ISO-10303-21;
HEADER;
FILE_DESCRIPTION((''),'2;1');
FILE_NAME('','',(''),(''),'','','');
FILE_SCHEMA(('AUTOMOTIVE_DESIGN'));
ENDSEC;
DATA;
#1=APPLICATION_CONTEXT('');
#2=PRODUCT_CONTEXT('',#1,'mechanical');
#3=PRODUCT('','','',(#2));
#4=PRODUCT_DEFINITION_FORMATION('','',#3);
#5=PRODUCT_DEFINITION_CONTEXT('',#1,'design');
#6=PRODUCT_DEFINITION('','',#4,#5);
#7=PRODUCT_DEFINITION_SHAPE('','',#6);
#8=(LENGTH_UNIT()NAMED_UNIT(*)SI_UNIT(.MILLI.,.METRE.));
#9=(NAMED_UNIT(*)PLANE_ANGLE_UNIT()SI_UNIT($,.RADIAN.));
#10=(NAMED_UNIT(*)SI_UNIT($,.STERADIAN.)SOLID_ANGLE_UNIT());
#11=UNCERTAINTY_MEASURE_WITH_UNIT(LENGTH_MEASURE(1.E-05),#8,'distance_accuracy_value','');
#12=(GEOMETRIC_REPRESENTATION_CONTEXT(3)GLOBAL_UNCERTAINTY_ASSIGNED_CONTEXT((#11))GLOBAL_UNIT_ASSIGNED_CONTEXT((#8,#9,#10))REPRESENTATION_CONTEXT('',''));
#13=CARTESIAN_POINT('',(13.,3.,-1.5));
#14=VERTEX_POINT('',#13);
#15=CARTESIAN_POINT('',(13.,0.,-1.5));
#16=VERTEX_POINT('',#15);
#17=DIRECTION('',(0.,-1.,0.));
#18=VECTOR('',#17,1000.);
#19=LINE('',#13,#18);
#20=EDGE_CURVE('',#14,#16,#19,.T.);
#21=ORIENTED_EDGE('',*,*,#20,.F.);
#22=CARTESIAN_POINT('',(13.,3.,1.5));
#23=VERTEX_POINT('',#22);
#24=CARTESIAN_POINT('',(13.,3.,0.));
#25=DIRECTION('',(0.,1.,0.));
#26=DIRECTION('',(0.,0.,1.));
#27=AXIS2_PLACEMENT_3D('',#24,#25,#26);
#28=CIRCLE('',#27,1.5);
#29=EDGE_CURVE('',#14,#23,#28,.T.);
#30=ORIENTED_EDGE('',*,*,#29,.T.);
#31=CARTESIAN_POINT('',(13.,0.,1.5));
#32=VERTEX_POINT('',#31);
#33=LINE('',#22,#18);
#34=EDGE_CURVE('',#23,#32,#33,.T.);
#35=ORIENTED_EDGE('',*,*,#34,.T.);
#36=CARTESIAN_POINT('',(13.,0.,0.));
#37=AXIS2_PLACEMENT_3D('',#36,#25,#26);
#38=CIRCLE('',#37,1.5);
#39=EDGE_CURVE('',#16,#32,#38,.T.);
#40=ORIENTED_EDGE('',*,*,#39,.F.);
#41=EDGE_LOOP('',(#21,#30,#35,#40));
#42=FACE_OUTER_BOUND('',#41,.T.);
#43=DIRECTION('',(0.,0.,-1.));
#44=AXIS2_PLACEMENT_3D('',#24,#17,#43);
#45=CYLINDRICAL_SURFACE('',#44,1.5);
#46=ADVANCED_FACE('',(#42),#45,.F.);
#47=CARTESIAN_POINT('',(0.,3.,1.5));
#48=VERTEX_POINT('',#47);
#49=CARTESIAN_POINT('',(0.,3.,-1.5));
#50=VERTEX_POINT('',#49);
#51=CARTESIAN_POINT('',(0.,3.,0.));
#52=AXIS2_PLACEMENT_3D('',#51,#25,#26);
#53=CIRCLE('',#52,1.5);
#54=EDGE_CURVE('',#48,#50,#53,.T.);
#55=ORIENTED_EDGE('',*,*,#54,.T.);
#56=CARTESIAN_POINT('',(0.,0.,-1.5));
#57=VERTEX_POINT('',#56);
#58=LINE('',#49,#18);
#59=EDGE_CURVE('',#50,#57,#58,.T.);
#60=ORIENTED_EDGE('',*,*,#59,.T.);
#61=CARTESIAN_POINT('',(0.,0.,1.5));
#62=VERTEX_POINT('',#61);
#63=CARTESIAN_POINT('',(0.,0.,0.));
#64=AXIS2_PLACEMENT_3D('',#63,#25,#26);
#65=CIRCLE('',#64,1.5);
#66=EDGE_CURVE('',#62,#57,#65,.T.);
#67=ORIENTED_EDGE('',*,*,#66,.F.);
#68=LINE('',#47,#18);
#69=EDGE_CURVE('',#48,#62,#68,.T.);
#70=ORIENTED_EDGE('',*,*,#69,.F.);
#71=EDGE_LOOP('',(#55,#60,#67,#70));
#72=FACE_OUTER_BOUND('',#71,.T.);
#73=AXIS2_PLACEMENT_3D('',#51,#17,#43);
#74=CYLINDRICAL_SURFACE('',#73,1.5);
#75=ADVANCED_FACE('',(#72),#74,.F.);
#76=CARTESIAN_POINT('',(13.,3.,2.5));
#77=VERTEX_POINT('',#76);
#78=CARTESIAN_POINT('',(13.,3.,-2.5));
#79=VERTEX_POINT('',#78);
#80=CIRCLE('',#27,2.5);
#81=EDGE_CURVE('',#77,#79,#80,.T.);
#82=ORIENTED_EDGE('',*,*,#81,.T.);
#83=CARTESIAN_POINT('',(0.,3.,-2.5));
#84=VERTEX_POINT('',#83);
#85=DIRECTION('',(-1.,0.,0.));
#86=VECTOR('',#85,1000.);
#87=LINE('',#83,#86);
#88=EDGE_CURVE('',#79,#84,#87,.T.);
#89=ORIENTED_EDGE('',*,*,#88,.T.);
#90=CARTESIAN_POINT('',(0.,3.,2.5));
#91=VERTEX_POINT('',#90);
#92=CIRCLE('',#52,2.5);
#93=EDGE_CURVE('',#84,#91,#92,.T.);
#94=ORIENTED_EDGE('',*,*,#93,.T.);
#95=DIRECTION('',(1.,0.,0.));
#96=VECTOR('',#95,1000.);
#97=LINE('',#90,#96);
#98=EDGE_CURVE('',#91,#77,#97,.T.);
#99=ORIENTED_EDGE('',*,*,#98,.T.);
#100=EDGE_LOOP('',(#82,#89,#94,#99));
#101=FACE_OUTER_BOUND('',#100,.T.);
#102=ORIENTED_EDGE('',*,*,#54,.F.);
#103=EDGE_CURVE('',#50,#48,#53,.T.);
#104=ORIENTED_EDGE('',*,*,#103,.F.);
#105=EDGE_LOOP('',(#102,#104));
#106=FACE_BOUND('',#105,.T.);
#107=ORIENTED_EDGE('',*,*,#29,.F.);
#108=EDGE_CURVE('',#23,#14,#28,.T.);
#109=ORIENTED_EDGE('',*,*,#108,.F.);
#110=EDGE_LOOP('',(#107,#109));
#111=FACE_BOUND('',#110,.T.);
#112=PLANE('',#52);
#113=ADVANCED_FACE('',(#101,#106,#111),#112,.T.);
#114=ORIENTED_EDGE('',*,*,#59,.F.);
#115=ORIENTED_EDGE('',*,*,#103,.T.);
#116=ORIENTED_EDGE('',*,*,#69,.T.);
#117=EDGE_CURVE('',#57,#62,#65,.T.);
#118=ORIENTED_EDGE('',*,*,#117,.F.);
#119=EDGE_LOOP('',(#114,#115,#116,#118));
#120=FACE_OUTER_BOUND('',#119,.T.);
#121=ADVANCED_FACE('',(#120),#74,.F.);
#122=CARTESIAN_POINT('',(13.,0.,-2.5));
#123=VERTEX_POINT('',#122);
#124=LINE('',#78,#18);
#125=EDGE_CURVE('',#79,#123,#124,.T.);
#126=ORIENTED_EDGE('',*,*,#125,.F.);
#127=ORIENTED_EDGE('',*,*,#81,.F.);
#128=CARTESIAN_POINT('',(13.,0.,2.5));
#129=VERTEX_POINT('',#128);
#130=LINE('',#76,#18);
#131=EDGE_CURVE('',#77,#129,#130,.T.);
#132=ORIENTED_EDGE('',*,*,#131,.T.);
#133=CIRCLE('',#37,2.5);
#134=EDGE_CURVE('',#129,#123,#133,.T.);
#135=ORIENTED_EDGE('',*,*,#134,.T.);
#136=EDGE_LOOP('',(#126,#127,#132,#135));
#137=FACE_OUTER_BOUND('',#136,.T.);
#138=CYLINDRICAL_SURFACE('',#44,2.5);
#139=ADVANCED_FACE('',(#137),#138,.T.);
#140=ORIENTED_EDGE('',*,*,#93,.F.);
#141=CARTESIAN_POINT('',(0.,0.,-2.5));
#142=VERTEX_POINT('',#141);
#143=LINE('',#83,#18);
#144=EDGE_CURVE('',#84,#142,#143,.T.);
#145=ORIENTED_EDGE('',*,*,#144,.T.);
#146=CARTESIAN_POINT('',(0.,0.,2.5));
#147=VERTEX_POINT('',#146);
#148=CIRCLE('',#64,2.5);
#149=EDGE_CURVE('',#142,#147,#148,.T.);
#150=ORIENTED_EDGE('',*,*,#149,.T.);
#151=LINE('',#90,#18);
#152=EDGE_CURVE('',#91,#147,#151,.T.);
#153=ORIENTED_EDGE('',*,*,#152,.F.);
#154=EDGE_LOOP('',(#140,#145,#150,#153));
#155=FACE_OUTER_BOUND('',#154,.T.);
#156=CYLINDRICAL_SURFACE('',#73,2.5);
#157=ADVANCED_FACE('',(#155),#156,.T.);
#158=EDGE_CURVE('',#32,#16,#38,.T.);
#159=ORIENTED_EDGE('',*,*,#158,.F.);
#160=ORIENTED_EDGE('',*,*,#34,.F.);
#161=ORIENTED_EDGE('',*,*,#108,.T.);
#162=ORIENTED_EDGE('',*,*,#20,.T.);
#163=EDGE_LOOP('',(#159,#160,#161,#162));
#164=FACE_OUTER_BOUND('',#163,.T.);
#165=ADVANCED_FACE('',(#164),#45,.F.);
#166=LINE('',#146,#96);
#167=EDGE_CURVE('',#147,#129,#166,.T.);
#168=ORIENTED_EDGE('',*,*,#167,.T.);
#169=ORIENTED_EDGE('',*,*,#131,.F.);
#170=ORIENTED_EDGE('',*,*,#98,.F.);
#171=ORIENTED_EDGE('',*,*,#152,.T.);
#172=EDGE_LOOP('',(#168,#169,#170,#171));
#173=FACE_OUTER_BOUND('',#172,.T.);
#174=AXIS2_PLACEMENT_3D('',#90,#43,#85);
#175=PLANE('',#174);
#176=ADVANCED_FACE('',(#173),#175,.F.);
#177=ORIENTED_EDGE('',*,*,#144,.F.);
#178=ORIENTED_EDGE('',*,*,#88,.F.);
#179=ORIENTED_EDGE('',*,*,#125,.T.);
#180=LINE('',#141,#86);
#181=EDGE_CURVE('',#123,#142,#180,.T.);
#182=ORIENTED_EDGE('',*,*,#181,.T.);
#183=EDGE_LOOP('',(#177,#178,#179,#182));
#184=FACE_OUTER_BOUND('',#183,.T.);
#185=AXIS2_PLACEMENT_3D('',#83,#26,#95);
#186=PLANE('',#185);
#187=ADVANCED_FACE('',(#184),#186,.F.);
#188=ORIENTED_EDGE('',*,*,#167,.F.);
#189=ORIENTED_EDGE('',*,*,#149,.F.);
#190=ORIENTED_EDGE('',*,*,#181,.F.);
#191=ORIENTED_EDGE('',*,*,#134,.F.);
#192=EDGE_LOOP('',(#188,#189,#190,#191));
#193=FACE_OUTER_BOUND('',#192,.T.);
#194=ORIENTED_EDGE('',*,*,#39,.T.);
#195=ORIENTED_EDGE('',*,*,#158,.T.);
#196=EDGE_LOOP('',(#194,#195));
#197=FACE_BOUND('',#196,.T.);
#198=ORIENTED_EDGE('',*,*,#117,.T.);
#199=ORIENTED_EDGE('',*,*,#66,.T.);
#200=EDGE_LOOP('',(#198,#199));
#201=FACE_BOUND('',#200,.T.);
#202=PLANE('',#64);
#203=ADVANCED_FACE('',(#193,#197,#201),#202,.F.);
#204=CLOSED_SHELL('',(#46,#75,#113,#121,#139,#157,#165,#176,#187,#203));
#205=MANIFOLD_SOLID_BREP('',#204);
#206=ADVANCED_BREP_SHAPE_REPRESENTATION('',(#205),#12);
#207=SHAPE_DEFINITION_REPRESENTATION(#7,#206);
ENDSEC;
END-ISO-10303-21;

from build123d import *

# Parameters (mm, degrees)
SKETCH1_R           = 1.5
BOSS_EXTRUDE1_DEPTH = 3


with BuildPart() as part:
    # Sketch1 → Boss-Extrude1 (new body)
    with BuildSketch(Plane(origin=(0, 0, 0), x_dir=(1, 0, 0), z_dir=(0, 1, 0))):
        with BuildLine():
            Line((0, 2.5), (13, 2.5))
            ThreePointArc((13, 2.5), (15.5, 0), (13, -2.5))
            Line((13, -2.5), (0, -2.5))
            ThreePointArc((0, -2.5), (-2.5, 0), (0, 2.5))
        make_face()
        with Locations(Location((0, 0, 0), (0, 0, 270))):
            Circle(SKETCH1_R, mode=Mode.SUBTRACT)
        with Locations(Location((13, 0, 0), (0, 0, 270))):
            Circle(SKETCH1_R, mode=Mode.SUBTRACT)
    extrude(amount=BOSS_EXTRUDE1_DEPTH)


solid = part.part
